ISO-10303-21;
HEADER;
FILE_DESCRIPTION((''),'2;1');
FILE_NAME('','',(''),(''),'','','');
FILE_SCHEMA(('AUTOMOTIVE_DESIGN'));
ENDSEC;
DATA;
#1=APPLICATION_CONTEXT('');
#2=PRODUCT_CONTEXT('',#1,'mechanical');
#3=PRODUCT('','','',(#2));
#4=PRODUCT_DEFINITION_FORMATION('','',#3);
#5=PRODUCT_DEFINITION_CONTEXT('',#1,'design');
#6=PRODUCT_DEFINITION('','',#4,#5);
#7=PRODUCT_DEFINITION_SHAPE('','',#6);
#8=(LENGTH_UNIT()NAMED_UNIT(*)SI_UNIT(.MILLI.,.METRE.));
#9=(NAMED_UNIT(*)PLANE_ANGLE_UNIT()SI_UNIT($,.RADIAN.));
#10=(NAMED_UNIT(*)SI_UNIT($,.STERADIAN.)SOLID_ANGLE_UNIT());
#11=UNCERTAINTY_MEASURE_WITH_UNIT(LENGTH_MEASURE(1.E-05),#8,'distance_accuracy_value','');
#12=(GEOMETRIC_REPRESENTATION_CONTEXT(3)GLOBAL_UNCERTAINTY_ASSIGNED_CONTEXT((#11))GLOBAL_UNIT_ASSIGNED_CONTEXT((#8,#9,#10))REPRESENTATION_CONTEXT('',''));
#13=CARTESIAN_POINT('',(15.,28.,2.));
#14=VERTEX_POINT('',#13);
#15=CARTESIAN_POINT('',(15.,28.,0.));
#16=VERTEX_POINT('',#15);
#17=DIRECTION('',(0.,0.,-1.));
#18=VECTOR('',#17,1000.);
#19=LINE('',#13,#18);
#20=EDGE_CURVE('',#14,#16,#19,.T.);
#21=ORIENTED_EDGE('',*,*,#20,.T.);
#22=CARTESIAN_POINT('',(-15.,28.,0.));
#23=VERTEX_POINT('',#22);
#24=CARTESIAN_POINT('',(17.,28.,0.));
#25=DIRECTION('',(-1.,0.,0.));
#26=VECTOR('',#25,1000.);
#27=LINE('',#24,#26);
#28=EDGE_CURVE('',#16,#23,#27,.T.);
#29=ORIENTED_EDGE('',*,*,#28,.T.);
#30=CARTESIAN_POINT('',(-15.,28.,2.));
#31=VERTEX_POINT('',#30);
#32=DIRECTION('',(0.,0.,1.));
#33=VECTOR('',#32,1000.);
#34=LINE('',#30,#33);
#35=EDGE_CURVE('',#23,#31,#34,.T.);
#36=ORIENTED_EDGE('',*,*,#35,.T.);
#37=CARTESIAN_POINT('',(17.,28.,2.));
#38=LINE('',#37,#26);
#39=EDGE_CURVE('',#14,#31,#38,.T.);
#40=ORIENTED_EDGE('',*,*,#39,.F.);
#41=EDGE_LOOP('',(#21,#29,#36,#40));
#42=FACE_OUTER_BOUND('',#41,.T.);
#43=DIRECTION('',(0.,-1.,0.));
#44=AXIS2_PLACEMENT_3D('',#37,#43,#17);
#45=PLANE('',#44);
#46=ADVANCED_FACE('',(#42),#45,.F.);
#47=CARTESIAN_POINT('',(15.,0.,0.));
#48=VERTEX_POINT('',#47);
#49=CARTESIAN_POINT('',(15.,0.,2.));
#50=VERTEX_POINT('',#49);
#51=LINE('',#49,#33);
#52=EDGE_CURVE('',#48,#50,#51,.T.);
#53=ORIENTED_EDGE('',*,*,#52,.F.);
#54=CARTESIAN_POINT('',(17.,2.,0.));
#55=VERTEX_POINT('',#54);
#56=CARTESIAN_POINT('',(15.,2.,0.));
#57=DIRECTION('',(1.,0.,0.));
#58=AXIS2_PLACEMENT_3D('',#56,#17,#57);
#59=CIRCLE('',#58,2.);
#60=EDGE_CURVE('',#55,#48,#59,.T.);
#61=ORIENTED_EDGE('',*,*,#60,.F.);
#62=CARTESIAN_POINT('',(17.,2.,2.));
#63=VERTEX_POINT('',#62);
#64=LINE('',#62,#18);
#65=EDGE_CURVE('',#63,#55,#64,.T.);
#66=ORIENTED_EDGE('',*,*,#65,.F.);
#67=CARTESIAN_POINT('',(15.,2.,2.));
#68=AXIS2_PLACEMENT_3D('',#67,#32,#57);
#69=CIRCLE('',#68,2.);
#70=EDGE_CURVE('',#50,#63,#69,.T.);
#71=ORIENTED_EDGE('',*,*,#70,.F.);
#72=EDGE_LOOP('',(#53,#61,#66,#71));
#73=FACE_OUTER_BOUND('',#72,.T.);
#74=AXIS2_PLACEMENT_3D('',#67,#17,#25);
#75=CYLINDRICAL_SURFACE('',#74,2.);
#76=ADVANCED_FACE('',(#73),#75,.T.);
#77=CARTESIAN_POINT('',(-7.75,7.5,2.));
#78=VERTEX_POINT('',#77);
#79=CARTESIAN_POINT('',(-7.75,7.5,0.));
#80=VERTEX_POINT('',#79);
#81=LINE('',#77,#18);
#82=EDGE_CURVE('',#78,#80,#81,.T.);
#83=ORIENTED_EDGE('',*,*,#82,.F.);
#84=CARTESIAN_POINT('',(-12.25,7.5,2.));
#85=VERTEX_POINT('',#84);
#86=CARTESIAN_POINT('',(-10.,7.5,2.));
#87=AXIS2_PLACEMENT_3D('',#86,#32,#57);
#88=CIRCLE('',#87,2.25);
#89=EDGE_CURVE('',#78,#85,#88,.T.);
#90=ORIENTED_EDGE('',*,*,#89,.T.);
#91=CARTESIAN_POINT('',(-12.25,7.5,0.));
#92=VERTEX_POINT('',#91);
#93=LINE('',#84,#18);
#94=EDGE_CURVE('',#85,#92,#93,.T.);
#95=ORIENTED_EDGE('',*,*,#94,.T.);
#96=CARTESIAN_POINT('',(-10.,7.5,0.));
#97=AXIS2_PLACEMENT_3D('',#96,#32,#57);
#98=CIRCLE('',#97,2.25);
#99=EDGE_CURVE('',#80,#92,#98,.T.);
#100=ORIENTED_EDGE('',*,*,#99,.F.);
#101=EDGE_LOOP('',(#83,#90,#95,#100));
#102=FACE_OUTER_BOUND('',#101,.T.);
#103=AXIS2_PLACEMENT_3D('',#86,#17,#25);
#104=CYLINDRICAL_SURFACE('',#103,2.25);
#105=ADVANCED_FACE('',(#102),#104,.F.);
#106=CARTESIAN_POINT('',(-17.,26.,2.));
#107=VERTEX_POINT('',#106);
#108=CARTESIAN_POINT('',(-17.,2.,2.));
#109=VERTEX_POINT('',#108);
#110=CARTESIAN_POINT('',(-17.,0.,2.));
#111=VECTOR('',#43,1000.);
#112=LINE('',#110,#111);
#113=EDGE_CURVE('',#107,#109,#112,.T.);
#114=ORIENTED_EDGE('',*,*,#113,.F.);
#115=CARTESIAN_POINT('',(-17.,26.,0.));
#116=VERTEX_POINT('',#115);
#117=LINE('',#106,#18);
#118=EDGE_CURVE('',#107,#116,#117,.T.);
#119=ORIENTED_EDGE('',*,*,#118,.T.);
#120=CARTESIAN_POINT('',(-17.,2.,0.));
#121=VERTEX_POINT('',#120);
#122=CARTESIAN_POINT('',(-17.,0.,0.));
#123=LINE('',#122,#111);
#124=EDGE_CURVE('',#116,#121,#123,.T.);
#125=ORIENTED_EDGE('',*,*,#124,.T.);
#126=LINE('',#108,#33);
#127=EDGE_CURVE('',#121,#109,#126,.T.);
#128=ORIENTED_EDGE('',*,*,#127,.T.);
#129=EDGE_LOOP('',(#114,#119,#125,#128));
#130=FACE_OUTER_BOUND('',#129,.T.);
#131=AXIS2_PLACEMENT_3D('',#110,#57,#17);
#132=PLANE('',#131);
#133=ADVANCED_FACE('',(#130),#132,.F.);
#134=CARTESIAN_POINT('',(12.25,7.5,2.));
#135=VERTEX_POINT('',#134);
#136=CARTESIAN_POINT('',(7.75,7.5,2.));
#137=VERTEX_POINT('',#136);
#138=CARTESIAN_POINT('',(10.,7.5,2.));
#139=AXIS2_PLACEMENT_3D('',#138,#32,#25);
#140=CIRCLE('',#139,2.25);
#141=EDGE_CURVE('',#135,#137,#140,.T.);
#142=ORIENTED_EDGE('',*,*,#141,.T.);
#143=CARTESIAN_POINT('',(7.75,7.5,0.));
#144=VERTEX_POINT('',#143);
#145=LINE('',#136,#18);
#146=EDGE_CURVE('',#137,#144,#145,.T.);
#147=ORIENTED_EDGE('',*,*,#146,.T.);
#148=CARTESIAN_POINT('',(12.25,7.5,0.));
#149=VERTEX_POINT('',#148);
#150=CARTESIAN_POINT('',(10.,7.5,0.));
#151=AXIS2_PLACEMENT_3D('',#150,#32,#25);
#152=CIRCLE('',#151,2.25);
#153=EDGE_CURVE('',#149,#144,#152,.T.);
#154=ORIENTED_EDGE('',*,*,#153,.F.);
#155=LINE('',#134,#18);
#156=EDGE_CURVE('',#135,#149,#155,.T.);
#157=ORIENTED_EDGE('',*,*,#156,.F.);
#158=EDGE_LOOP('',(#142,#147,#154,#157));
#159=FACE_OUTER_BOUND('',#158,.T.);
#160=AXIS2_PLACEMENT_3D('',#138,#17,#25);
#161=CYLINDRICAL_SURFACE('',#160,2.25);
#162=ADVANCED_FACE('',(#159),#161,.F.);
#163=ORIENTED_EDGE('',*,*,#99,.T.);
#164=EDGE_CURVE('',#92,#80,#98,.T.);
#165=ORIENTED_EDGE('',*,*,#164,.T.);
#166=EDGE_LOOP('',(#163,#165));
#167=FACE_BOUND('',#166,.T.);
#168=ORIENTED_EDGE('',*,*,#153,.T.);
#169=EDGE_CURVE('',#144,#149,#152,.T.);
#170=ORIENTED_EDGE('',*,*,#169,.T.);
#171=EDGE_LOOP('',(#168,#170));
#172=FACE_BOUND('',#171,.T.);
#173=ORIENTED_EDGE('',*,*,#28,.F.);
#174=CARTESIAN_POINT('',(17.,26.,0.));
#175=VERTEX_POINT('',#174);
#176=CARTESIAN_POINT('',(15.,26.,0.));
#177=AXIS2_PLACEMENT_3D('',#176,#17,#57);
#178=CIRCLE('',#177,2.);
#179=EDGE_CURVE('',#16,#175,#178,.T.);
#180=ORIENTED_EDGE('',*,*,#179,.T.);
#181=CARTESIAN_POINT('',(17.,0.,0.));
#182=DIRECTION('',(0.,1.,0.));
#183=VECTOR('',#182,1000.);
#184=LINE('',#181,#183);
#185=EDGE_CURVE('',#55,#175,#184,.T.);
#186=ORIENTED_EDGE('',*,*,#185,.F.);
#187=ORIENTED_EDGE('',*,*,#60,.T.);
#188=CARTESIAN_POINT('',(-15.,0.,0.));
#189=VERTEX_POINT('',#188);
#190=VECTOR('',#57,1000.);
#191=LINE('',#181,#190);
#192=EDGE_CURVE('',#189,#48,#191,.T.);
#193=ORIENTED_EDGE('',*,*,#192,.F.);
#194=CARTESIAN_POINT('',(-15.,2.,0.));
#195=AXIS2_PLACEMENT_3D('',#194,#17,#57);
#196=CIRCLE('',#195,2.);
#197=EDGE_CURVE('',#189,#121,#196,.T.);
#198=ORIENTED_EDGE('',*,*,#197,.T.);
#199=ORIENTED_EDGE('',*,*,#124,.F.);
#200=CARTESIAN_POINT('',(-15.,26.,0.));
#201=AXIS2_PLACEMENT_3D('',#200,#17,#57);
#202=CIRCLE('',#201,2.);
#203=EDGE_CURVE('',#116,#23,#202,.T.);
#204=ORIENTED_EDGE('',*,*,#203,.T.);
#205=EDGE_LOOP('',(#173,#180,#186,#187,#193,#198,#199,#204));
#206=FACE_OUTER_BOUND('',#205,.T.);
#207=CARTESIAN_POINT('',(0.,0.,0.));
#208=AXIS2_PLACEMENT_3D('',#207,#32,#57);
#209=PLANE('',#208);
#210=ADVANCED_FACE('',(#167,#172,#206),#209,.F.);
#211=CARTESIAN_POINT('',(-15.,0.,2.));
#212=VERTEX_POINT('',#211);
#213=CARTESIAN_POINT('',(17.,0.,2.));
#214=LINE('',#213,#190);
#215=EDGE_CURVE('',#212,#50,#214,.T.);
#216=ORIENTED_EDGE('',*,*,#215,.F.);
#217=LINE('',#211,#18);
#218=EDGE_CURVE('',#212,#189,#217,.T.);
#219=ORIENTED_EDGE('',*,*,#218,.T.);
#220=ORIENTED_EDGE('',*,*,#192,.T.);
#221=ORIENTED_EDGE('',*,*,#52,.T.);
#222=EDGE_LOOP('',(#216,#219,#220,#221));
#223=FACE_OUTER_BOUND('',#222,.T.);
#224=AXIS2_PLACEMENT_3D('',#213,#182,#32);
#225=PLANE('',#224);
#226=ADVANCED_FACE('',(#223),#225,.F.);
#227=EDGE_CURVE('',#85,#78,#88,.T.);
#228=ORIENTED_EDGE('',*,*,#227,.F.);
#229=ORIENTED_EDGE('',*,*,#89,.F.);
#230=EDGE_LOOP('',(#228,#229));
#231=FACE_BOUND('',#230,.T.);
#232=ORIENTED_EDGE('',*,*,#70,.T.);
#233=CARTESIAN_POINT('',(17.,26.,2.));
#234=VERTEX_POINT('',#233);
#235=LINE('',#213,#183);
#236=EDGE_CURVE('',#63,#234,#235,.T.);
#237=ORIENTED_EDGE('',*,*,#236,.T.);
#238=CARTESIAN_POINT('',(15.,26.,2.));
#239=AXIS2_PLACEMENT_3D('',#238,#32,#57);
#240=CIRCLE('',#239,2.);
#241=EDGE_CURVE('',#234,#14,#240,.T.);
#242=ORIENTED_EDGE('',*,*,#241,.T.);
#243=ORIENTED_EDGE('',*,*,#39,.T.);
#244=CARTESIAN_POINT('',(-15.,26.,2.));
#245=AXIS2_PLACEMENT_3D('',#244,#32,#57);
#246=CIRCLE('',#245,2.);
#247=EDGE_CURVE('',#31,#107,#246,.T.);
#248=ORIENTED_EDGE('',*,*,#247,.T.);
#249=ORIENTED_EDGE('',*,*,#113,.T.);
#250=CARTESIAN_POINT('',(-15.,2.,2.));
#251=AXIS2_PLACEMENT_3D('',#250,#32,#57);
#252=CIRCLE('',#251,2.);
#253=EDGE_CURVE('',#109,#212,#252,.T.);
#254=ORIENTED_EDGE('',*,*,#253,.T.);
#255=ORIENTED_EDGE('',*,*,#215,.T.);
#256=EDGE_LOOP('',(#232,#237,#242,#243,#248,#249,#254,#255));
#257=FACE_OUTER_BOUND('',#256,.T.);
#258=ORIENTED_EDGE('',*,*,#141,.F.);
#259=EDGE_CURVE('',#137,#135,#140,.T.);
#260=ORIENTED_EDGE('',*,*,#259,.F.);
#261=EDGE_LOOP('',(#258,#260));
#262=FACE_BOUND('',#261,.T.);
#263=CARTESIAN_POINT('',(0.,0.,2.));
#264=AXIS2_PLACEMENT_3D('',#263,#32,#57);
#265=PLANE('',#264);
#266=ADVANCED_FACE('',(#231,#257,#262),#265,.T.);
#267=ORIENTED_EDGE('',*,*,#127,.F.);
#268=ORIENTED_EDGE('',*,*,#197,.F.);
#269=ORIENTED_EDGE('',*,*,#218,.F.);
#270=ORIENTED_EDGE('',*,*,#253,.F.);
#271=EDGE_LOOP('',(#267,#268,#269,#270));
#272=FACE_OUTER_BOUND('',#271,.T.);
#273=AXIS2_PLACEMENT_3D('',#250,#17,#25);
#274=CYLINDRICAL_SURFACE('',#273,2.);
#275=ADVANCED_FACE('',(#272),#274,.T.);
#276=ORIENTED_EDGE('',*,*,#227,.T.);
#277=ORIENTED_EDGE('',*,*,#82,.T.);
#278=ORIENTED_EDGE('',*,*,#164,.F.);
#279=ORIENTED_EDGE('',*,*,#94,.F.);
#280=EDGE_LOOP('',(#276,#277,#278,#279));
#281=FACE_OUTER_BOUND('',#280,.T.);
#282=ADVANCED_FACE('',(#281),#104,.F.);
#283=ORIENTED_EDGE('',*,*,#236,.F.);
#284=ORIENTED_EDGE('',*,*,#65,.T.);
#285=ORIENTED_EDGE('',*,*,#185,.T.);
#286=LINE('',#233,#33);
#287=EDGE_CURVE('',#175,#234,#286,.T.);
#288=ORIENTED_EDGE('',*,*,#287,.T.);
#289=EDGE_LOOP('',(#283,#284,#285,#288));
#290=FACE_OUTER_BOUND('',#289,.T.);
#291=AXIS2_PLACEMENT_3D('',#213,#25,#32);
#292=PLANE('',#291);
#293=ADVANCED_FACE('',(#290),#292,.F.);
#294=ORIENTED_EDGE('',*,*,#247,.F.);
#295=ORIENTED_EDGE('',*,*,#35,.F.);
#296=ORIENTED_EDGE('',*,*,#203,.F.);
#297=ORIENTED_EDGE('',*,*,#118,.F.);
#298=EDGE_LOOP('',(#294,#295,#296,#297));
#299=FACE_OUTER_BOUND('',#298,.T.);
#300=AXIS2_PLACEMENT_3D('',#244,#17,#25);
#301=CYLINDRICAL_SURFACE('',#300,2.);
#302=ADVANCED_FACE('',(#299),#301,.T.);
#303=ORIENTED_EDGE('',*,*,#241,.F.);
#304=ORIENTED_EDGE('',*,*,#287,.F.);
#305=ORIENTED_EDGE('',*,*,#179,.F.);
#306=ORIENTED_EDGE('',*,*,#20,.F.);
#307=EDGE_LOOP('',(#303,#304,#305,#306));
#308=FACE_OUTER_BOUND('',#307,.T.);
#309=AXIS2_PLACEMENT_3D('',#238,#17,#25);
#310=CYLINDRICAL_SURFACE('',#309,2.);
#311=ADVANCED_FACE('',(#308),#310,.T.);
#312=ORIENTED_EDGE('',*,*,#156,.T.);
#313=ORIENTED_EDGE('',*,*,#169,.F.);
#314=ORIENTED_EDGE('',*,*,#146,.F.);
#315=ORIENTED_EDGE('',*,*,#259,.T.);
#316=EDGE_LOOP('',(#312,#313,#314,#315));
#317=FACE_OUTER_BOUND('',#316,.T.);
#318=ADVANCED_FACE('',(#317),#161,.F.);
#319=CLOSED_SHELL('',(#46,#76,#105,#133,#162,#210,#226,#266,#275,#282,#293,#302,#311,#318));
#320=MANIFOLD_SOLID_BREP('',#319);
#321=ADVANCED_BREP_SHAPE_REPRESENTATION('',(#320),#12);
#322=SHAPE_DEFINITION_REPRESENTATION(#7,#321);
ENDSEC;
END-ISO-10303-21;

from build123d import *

# Parameters (mm, degrees)
SKETCH1_W           = 34
SKETCH1_H           = 28
SKETCH1_R           = 2.25
BOSS_EXTRUDE1_DEPTH = 2
FILLET1_R           = 2


with BuildPart() as part:
    # Sketch1 → Boss-Extrude1 (new body)
    with BuildSketch(Plane.XY):
        with Locations((0, 14)):
            Rectangle(SKETCH1_W, SKETCH1_H)
        with Locations((-10, 7.5)):
            Circle(SKETCH1_R, mode=Mode.SUBTRACT)
        with Locations(Location((10, 7.5, 0), (0, 0, 180))):
            Circle(SKETCH1_R, mode=Mode.SUBTRACT)
    extrude(amount=BOSS_EXTRUDE1_DEPTH)

    # Fillet1
    fillet1_edges = [part.edges().sort_by_distance(p)[0] for p in [
        (17, 0, 1),
        (-17, 0, 1),
        (-17, 28, 1),
        (17, 28, 1),
    ]]
    fillet(fillet1_edges, radius=FILLET1_R)


solid = part.part
